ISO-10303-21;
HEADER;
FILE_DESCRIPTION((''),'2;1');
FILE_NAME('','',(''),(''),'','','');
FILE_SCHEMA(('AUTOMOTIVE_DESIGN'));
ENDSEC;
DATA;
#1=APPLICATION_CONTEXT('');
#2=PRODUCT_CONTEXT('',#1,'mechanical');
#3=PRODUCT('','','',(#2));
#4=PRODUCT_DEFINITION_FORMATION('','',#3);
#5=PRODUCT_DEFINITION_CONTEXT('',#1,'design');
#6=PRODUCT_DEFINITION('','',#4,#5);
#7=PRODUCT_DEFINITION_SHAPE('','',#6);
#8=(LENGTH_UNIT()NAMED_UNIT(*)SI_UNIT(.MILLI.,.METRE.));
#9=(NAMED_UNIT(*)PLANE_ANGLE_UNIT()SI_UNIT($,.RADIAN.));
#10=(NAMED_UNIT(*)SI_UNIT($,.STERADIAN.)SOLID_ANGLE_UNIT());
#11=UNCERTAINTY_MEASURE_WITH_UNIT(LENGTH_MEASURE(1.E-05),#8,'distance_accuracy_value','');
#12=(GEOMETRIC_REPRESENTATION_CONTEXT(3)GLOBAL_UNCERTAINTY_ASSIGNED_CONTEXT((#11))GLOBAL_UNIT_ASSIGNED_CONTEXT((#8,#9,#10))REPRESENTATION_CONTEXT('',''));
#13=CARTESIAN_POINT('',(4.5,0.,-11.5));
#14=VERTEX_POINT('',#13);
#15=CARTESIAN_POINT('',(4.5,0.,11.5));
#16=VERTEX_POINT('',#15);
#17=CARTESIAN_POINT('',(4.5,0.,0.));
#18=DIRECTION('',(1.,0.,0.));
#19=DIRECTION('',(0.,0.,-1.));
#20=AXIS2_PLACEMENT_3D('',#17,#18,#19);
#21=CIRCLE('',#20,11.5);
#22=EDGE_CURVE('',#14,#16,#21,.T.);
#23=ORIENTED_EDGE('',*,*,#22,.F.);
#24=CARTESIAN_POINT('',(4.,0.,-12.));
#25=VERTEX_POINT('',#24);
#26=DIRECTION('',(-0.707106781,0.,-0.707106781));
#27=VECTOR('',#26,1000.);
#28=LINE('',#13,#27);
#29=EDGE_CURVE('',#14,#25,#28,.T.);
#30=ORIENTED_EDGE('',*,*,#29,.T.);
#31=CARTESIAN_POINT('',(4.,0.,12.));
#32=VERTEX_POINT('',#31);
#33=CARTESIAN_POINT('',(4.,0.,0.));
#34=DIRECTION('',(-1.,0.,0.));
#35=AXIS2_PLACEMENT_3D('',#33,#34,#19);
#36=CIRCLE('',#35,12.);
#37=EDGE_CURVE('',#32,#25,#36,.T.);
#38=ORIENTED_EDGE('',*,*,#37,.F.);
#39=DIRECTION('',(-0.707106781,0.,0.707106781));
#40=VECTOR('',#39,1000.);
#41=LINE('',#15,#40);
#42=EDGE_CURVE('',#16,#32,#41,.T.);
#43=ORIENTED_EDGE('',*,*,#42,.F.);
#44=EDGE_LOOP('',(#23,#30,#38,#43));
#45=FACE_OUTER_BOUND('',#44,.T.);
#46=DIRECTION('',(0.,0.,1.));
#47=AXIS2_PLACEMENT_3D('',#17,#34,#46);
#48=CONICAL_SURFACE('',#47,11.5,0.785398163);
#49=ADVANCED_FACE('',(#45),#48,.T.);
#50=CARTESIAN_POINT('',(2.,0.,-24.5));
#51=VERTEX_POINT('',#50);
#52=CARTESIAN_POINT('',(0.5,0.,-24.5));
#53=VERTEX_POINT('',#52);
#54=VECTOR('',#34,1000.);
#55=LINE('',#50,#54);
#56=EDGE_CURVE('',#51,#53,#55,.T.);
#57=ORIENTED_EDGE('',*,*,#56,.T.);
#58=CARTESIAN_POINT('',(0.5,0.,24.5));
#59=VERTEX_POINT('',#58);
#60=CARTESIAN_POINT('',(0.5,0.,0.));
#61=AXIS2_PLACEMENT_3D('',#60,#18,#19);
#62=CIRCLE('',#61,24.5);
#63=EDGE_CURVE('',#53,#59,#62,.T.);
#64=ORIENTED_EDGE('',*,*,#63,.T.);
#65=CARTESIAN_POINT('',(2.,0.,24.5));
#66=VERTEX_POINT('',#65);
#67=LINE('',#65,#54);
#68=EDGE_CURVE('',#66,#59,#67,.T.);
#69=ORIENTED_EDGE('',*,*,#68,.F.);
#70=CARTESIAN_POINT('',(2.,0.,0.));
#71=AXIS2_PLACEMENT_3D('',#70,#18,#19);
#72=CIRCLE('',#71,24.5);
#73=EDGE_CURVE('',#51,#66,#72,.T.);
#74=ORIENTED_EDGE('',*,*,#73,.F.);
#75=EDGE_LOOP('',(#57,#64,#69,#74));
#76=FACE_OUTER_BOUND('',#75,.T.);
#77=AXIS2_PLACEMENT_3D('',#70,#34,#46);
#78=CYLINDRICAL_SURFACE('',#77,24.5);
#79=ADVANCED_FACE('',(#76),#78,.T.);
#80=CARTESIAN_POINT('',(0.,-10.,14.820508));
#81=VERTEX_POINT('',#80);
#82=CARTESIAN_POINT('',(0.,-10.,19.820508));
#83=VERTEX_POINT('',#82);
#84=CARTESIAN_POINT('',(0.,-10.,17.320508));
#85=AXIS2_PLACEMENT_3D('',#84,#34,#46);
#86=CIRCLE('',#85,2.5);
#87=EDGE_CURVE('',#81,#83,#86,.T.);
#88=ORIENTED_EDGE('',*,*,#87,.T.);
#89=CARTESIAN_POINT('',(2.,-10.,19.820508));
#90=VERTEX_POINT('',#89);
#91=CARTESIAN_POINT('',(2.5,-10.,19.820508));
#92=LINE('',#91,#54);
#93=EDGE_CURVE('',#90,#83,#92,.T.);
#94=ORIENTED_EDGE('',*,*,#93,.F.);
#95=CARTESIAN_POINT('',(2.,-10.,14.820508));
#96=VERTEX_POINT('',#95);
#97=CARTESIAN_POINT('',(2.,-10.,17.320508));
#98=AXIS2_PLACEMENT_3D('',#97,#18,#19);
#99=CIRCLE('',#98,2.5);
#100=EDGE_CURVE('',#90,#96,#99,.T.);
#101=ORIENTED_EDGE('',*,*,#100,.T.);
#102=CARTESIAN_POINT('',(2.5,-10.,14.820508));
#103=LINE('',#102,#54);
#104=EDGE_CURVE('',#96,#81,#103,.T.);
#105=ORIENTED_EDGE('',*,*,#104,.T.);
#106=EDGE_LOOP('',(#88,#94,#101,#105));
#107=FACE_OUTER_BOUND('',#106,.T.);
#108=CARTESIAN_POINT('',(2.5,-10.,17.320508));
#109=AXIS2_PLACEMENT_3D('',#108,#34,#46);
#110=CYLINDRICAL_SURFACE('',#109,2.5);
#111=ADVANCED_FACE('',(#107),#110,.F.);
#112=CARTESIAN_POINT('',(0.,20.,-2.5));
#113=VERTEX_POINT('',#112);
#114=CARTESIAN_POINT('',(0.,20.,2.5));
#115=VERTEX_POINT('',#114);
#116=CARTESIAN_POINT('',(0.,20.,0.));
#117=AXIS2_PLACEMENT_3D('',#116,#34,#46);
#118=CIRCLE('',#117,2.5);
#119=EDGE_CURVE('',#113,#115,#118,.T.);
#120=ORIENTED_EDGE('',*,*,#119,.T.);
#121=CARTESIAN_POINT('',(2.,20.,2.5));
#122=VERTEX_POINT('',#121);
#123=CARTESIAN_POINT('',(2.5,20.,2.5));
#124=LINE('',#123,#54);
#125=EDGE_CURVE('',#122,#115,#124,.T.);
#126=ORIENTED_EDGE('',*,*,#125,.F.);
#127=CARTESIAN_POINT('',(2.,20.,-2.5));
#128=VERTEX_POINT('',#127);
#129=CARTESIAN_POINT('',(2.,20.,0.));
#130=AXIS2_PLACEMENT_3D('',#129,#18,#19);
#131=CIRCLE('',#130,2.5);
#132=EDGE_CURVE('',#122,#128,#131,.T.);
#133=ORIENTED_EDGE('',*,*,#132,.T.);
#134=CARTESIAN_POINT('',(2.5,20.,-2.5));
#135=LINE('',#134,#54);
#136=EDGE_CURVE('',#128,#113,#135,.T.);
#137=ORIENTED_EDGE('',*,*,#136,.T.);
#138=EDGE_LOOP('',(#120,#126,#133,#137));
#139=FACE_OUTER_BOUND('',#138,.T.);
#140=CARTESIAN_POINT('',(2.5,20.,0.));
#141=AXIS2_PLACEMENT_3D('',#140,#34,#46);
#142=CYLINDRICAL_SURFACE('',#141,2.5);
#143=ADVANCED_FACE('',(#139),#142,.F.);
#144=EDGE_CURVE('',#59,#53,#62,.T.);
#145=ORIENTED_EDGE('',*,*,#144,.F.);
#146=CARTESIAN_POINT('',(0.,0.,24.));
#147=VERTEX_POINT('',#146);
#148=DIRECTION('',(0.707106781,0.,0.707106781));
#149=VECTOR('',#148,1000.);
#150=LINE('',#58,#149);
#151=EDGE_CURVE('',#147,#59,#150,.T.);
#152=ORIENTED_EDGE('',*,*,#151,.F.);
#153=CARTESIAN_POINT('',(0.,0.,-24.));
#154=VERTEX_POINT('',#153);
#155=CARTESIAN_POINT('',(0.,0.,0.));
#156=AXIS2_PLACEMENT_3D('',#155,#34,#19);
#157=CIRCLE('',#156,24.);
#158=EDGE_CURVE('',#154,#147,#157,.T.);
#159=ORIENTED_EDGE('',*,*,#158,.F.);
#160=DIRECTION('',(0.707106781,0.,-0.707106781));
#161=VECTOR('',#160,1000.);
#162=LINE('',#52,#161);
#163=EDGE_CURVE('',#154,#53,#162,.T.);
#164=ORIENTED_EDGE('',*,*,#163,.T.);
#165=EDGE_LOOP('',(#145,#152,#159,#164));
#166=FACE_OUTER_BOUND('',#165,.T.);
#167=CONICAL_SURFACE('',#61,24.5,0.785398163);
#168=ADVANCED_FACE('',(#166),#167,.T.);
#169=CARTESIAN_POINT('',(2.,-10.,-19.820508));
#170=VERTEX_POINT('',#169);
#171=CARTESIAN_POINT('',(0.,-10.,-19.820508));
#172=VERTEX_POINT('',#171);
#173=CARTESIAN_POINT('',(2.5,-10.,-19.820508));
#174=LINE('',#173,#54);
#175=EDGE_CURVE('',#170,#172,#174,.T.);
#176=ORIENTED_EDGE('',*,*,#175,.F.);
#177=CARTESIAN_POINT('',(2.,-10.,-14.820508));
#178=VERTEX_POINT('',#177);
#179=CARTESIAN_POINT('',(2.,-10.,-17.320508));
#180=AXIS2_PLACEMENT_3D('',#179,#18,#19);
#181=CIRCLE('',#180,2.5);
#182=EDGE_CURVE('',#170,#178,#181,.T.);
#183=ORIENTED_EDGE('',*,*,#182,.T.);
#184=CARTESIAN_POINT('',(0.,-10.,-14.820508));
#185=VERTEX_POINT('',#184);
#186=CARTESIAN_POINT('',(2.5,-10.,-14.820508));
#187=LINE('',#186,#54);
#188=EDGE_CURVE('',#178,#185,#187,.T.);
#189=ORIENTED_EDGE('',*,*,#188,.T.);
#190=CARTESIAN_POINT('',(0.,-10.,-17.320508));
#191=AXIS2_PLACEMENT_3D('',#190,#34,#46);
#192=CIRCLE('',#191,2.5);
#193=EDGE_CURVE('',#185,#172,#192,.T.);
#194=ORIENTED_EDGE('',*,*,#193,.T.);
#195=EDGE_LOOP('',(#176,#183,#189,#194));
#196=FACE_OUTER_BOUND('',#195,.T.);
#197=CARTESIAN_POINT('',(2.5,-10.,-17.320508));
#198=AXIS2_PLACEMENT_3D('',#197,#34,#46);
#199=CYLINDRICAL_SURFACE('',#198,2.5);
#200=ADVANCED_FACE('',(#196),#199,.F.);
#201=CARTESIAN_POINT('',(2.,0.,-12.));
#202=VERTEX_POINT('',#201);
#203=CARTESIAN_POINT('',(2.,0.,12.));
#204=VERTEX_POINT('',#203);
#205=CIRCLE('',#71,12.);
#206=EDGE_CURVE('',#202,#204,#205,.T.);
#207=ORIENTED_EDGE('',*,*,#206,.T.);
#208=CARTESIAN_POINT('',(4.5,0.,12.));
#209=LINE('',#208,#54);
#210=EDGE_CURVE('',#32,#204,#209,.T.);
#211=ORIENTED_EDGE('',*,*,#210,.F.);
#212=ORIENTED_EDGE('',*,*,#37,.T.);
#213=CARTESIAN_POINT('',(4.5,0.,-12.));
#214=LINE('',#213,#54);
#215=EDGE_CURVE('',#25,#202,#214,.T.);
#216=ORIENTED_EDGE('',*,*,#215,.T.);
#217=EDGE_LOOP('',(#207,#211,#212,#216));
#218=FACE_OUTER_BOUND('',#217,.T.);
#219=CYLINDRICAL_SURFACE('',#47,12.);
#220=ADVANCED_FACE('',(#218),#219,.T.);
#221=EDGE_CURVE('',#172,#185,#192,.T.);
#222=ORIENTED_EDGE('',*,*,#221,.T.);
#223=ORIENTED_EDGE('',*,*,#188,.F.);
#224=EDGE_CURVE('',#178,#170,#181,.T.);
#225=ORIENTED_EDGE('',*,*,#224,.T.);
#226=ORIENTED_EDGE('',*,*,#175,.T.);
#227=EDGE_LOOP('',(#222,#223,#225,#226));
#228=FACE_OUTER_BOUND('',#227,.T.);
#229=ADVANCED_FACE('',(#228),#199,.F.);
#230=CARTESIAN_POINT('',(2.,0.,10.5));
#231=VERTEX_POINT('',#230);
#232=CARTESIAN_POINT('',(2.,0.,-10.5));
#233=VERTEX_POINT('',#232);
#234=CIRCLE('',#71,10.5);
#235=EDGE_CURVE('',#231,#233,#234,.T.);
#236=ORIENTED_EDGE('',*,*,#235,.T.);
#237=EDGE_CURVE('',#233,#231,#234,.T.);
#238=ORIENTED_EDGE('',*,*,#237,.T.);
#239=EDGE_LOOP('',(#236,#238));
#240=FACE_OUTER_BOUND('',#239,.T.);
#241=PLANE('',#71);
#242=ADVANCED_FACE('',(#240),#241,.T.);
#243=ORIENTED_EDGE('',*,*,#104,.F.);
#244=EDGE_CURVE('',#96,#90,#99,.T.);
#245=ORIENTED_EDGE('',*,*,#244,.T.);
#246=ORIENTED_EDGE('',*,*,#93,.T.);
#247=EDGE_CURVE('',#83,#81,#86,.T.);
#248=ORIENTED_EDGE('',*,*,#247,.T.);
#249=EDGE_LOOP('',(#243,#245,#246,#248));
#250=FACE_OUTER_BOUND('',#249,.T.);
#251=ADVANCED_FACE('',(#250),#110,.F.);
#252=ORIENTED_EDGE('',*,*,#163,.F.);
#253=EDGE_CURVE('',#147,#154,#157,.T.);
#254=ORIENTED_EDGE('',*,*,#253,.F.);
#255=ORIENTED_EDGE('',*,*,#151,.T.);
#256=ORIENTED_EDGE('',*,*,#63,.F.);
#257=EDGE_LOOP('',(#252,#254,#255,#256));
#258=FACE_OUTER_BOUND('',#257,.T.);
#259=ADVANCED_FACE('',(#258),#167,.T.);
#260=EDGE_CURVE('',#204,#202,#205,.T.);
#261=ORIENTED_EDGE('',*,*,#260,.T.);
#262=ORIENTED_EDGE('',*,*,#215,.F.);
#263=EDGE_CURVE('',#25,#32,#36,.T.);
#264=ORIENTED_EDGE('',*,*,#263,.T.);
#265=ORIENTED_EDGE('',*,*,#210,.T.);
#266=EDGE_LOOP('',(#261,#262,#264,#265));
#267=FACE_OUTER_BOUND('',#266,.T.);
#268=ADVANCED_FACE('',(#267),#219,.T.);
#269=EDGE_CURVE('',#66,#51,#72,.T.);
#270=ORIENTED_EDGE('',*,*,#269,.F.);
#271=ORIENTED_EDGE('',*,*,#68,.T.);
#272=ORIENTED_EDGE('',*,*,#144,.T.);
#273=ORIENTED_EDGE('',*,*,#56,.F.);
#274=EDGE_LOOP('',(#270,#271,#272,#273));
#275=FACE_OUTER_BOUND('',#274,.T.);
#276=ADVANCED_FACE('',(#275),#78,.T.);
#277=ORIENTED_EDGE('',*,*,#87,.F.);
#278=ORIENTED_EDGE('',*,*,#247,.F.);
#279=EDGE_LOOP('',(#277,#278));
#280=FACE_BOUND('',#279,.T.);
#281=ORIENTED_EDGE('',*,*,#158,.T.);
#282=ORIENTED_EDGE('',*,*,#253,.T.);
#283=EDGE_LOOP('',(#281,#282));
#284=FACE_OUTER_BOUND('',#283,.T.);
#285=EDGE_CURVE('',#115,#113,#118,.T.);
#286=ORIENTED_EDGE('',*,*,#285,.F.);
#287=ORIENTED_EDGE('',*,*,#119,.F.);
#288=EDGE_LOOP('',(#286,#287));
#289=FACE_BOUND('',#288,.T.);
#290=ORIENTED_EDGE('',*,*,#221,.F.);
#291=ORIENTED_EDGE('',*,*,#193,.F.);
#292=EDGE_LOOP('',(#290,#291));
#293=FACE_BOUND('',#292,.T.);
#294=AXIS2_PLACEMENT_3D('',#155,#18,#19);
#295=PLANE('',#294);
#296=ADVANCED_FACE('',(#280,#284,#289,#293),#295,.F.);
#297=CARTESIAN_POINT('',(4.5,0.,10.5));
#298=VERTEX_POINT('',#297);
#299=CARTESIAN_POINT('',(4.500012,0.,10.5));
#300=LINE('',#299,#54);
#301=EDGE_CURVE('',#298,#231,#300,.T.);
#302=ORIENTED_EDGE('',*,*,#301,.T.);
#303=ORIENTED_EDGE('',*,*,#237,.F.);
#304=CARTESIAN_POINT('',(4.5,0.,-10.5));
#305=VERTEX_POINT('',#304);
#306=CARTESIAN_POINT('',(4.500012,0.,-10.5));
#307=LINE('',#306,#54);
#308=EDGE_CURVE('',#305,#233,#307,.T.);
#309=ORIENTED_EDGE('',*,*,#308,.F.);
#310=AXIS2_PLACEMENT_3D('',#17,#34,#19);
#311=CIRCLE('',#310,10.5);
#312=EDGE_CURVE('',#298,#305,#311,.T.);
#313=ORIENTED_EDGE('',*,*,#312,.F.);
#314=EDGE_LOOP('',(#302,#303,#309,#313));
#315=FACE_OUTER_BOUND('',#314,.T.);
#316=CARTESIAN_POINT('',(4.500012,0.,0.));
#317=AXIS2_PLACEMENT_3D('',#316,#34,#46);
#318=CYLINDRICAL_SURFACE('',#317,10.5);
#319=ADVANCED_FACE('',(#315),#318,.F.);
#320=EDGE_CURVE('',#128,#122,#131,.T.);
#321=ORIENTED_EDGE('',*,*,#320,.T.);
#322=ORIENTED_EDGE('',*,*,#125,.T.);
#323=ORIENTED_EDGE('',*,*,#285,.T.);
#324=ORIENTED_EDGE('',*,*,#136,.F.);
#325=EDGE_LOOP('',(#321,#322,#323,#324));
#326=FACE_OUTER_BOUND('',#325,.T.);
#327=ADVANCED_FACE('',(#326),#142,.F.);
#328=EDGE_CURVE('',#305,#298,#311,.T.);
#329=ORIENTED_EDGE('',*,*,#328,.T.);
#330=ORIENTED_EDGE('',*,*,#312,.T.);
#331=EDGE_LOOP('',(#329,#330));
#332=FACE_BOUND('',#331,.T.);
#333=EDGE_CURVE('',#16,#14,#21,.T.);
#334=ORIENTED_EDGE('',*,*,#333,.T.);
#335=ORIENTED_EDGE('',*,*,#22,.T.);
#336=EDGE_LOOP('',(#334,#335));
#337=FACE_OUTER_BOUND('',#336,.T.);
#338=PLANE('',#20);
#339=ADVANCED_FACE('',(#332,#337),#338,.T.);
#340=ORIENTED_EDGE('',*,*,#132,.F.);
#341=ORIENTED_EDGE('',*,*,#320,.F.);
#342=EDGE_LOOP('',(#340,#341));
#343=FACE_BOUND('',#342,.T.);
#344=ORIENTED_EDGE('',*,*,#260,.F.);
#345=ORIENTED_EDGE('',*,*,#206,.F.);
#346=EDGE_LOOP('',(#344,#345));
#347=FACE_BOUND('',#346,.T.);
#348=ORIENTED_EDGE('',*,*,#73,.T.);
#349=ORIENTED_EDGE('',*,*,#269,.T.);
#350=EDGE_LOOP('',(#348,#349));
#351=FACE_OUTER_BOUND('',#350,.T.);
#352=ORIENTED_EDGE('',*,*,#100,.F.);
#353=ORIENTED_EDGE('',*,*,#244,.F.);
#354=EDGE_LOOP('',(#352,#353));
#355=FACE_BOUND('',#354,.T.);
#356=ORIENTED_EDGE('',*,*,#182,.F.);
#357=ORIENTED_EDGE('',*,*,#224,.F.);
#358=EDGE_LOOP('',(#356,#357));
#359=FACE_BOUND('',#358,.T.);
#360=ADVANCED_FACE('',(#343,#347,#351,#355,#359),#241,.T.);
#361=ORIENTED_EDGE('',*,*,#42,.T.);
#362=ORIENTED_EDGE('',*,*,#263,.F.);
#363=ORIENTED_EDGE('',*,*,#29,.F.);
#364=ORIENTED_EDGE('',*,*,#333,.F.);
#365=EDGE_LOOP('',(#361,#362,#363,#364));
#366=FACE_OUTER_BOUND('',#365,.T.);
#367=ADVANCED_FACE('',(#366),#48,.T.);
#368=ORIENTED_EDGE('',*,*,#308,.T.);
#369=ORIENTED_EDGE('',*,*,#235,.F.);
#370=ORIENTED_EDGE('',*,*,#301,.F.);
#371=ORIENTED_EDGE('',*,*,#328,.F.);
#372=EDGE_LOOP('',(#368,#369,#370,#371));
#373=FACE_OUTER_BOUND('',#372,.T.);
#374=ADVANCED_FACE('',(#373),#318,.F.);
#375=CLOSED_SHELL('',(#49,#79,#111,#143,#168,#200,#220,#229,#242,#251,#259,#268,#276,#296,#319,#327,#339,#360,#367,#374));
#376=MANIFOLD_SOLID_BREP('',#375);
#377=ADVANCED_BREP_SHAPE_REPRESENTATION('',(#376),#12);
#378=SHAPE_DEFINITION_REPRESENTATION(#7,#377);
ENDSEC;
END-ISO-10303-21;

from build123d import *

# Parameters (mm, degrees)
SKETCH1_R               = 24.5
BOSS_EXTRUDE1_DEPTH     = 2
SKETCH2_R               = 12
BOSS_EXTRUDE2_DEPTH     = 2.5
CUT_EXTRUDE1_DEPTH      = 35.939232962
CUT_EXTRUDE1_DEPTH_BACK = 2.5
SKETCH3_R               = 10.5
SKETCH4_R               = 2.5
CUT_EXTRUDE2_DEPTH      = 2.5
CHAMFER1_SIZE           = 0.5


with BuildPart() as part:
    # Sketch1 → Boss-Extrude1 (new body)
    with BuildSketch(Plane(origin=(0, 0, 0), x_dir=(0, 0, -1), z_dir=(1, 0, 0))):
        Circle(SKETCH1_R)
    extrude(amount=BOSS_EXTRUDE1_DEPTH)

    # Sketch2 → Boss-Extrude2 (add)
    with BuildSketch(Plane(origin=(2, 0, 0), x_dir=(0, 0, -1), z_dir=(1, 0, 0))):
        Circle(SKETCH2_R)
    extrude(amount=BOSS_EXTRUDE2_DEPTH)

    # Sketch3 → Cut-Extrude1 (cut, two sides: drawn at the far end of the back side and taken through both)
    with BuildSketch(Plane(origin=(4.5, 0, 0), x_dir=(0, 0, -1), z_dir=(1, 0, 0)).offset(-CUT_EXTRUDE1_DEPTH_BACK)):
        with Locations(Location((0, 0, 0), (0, 0, 180))):
            Circle(SKETCH3_R)
    extrude(amount=CUT_EXTRUDE1_DEPTH + CUT_EXTRUDE1_DEPTH_BACK, mode=Mode.SUBTRACT)

    # Sketch4 → Cut-Extrude2 (cut)
    with BuildSketch(Plane.ZY):
        with Locations((0, 20)):
            Circle(SKETCH4_R)
        with Locations((17.320508076, -10)):
            Circle(SKETCH4_R)
        with Locations((-17.320508076, -10)):
            Circle(SKETCH4_R)
    extrude(amount=-CUT_EXTRUDE2_DEPTH, mode=Mode.SUBTRACT)

    # Chamfer1
    chamfer1_edges = [part.edges().sort_by_distance(p)[0] for p in [
        (0, 0, 24.5),
        (4.5, 0, 12),
    ]]
    chamfer(chamfer1_edges, length=CHAMFER1_SIZE)


solid = part.part
